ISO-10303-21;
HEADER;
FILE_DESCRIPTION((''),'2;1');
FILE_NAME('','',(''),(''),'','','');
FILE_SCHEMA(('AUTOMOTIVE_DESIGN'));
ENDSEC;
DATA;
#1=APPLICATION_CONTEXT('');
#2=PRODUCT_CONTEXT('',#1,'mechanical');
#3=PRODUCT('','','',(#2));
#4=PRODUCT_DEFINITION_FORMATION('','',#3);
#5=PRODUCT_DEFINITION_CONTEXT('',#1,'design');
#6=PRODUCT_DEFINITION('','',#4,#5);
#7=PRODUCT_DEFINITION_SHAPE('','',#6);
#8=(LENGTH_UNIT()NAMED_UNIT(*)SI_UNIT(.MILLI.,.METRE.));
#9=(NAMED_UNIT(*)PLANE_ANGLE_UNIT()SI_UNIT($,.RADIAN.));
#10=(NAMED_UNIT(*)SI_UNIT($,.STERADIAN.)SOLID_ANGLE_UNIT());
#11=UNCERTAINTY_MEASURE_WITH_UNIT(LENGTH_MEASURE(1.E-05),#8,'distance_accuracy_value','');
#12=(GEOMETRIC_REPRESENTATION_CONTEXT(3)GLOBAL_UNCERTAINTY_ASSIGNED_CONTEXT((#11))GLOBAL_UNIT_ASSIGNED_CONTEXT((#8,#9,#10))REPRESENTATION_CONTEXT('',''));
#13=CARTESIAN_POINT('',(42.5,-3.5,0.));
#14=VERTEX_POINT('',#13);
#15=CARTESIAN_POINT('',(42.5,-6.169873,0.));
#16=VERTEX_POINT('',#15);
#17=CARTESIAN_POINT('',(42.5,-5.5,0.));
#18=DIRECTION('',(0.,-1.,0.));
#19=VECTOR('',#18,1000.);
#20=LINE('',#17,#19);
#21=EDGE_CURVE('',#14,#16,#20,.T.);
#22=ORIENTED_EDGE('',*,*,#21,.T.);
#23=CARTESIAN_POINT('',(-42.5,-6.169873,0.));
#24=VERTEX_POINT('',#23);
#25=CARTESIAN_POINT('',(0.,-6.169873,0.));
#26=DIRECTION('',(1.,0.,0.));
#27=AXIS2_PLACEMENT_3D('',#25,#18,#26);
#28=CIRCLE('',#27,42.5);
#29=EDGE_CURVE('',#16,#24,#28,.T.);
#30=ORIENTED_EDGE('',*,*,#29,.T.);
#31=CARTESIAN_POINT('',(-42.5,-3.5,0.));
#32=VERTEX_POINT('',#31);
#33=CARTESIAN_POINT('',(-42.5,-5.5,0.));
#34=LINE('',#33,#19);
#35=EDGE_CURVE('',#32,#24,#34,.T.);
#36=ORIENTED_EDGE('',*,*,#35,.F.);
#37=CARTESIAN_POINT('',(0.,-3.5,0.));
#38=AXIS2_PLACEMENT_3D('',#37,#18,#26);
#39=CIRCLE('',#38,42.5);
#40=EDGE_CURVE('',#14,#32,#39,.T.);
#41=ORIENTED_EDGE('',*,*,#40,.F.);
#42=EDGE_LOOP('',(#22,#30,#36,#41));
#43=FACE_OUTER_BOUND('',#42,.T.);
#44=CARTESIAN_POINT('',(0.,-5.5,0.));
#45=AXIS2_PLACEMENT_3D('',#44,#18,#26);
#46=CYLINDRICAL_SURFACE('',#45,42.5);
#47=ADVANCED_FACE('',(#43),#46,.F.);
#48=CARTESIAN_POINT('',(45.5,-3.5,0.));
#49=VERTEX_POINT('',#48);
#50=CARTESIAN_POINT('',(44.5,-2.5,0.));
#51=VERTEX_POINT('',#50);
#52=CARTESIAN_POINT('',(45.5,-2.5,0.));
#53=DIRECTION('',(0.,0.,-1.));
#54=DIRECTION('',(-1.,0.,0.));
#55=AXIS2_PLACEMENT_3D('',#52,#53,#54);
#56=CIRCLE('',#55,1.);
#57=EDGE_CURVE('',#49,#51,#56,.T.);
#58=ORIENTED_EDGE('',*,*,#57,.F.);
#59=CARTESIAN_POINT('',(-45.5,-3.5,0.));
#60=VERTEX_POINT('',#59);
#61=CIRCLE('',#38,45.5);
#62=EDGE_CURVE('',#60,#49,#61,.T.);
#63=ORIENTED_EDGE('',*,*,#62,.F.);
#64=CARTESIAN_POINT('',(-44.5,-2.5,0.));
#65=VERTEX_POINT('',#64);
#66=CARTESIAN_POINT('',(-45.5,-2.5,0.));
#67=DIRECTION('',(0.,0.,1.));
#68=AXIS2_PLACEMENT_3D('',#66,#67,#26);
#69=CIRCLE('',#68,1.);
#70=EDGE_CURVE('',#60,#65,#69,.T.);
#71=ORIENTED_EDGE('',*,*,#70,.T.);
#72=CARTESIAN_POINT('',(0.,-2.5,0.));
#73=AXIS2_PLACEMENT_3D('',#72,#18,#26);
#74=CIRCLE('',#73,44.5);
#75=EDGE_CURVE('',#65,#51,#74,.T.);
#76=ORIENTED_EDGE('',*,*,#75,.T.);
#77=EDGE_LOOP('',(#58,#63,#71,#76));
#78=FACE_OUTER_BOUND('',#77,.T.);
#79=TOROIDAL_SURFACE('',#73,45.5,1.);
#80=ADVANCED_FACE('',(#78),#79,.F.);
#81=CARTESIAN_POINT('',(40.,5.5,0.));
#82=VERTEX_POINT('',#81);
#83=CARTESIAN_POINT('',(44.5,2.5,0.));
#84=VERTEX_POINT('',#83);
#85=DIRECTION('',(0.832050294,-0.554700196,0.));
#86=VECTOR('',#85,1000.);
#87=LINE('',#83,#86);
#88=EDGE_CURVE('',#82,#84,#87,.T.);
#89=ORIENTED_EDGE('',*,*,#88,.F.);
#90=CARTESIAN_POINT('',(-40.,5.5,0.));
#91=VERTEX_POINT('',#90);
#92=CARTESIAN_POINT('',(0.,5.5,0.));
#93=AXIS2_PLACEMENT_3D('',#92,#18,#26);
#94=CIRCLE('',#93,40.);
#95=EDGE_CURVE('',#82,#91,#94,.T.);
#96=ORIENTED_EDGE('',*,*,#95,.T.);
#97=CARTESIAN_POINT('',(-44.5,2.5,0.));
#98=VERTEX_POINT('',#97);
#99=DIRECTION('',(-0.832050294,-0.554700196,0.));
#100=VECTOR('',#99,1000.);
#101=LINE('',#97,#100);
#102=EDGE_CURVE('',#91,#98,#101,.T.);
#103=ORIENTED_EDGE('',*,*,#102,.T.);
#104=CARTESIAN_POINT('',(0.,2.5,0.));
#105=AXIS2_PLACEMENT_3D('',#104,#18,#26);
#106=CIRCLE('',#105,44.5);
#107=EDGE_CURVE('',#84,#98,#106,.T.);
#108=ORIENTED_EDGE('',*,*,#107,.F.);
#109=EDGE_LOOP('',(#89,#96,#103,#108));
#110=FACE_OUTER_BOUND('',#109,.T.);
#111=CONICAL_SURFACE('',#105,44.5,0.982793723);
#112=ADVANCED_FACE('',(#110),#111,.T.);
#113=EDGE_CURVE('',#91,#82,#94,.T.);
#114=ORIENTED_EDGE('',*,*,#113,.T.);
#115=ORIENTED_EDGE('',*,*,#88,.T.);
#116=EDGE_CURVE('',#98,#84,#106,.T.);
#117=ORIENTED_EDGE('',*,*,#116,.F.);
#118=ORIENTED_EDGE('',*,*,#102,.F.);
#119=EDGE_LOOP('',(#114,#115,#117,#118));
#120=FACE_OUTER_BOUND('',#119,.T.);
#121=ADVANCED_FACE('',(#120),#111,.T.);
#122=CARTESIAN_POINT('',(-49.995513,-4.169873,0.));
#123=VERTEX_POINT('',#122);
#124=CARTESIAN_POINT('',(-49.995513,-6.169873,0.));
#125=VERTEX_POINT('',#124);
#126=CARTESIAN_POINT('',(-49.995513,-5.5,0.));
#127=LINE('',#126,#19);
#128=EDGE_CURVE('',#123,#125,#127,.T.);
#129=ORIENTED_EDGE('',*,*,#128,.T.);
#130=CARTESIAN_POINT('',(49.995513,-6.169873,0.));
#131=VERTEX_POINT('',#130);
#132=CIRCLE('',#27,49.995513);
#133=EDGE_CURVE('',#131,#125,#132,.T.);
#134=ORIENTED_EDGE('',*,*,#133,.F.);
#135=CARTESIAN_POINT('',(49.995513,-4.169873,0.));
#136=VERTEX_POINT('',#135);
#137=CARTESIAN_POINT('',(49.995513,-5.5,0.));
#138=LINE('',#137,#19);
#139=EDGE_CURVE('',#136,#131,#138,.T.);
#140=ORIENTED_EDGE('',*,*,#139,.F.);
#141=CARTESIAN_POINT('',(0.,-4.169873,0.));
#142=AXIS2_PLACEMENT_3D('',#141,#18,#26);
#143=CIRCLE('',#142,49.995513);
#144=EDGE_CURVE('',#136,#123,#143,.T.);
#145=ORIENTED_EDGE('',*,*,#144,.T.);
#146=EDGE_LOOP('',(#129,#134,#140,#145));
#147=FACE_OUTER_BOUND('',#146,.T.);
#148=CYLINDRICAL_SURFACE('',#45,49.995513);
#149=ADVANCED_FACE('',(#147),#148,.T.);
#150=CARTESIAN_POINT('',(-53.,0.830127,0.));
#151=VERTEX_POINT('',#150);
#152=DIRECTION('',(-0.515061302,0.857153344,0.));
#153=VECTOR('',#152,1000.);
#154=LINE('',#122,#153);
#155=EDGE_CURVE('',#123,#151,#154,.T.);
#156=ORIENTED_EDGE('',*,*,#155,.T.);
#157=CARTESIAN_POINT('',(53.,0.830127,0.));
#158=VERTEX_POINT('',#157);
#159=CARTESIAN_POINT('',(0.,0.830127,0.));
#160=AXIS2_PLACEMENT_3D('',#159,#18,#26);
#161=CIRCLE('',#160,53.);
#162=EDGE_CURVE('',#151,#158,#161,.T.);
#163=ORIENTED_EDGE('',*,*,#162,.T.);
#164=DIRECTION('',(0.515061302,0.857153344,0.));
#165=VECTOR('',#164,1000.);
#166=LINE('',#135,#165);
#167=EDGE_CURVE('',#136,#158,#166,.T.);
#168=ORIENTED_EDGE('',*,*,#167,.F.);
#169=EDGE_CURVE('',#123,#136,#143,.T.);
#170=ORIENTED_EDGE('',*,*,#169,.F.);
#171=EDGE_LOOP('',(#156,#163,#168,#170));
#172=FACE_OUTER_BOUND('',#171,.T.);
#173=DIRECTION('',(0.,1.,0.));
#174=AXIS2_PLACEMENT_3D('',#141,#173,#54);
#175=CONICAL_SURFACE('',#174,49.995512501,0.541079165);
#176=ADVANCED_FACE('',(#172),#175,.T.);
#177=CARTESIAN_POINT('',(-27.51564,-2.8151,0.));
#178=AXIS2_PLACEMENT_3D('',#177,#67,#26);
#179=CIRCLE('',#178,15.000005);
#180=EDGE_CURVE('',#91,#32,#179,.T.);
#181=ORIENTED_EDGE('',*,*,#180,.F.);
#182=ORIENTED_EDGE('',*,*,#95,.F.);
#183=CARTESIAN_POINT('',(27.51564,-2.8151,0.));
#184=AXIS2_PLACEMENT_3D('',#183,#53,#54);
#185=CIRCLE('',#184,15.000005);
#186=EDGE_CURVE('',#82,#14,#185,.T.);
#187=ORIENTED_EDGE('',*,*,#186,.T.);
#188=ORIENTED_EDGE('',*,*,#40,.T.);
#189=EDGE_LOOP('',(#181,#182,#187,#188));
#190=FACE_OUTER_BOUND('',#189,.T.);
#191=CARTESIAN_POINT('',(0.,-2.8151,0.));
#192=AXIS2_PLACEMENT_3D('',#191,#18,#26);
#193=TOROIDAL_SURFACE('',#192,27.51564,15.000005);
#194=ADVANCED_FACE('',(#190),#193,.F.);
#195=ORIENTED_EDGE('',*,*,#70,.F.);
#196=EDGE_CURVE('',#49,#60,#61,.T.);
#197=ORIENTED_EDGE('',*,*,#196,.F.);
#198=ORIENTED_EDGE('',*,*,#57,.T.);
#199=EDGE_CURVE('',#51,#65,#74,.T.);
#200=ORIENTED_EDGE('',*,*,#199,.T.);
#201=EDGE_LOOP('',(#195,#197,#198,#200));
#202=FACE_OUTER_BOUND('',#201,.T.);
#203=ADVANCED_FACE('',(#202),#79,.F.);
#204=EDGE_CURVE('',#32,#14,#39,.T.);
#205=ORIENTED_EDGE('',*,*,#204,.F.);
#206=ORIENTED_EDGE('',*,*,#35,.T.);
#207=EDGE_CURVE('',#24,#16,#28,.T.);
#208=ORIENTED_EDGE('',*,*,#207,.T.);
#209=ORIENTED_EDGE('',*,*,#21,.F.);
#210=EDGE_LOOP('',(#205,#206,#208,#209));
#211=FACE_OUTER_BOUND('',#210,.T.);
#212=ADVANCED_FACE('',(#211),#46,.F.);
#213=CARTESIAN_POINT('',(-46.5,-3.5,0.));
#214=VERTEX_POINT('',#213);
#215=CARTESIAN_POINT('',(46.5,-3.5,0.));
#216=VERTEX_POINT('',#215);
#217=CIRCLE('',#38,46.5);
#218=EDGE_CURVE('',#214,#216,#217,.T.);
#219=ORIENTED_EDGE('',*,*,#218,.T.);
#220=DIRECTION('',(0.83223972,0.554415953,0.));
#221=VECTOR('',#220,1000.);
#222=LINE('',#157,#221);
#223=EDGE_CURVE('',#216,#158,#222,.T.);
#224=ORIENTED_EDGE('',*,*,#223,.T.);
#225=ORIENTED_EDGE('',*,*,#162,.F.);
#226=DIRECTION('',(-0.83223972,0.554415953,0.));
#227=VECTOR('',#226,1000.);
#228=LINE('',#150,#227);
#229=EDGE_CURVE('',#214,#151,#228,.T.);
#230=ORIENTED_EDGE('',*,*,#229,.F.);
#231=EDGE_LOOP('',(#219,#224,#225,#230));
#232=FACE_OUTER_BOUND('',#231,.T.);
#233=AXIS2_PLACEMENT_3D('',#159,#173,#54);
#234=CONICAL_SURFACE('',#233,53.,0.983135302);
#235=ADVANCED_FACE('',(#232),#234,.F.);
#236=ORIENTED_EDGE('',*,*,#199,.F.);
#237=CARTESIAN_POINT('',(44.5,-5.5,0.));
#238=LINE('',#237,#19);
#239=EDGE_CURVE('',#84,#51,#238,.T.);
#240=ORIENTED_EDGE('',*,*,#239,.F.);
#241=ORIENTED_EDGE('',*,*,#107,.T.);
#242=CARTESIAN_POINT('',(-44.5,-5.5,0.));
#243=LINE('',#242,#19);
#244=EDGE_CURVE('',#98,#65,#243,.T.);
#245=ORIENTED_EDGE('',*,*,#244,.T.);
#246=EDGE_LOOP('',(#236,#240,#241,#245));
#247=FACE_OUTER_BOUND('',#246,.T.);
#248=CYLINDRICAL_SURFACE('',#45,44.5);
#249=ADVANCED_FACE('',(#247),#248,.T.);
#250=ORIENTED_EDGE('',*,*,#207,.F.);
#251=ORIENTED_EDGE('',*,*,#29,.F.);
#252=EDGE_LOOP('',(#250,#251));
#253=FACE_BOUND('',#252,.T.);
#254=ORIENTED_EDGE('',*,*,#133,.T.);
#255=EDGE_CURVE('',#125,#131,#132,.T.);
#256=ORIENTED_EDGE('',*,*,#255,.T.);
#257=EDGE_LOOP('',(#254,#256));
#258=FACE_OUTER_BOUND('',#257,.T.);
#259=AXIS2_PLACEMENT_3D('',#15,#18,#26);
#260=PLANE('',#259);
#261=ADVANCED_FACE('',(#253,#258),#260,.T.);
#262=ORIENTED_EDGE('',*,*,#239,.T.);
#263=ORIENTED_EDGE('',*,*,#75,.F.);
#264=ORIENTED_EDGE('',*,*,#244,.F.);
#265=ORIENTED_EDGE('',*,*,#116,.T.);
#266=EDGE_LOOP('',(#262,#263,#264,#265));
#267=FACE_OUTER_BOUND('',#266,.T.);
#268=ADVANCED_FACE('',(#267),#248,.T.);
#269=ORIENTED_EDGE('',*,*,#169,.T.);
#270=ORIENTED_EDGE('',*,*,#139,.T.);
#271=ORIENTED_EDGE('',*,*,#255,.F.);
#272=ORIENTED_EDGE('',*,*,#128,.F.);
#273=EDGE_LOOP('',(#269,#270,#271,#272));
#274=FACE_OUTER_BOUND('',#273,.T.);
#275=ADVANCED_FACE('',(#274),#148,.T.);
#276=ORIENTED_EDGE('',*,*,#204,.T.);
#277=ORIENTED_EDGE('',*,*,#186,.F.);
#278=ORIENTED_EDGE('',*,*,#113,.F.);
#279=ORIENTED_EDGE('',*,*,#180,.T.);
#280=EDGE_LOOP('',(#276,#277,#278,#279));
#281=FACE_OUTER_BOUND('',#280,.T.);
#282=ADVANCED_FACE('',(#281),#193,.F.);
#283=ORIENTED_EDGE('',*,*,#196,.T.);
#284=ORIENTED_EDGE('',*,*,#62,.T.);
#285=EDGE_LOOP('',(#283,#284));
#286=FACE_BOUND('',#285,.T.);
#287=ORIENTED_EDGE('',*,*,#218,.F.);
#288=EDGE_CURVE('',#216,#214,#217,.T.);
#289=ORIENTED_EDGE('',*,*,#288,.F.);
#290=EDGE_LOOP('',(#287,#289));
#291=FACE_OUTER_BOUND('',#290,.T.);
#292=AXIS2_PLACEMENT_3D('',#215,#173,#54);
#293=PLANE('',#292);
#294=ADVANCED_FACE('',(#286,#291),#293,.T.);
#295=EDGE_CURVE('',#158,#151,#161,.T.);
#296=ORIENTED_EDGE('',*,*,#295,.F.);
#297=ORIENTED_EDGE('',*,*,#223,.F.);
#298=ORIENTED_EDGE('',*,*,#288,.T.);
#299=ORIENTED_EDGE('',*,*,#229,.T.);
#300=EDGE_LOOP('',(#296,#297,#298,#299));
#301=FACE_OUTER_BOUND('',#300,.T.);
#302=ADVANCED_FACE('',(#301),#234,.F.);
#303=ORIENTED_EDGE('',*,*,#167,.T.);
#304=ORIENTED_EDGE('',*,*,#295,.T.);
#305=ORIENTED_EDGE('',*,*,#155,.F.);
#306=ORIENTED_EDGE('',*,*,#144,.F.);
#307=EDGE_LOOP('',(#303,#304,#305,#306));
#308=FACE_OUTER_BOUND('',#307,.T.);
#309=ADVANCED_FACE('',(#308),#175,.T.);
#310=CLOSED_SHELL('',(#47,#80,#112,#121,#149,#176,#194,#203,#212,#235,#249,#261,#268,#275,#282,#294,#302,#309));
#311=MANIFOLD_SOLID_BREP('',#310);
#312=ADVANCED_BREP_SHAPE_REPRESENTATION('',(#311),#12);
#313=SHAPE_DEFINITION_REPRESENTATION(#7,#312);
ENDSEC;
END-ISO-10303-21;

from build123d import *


with BuildPart() as part:
    # 草图1 → 旋转1 (revolve)
    with BuildSketch(Plane.XY):
        with BuildLine():
            Line((42.5, -6.169872981), (49.995512501, -6.169872981))
            Line((49.995512501, -6.169872981), (49.995512501, -4.169872981))
            Line((49.995512501, -4.169872981), (53, 0.830127019))
            Line((53, 0.830127019), (46.5, -3.5))
            Line((46.5, -3.5), (45.5, -3.5))
            ThreePointArc((45.5, -3.5), (44.792893219, -3.207106781), (44.5, -2.5))
            Line((44.5, -2.5), (44.5, 2.5))
            Line((44.5, 2.5), (40, 5.5))
            ThreePointArc((40, 5.5), (41.968412898, 1.199559138), (42.5, -3.5))
            Line((42.5, -3.5), (42.5, -6.169872981))
        make_face()
    revolve(axis=Axis((0, -5.5, 0), (0, 1, 0)))


solid = part.part
